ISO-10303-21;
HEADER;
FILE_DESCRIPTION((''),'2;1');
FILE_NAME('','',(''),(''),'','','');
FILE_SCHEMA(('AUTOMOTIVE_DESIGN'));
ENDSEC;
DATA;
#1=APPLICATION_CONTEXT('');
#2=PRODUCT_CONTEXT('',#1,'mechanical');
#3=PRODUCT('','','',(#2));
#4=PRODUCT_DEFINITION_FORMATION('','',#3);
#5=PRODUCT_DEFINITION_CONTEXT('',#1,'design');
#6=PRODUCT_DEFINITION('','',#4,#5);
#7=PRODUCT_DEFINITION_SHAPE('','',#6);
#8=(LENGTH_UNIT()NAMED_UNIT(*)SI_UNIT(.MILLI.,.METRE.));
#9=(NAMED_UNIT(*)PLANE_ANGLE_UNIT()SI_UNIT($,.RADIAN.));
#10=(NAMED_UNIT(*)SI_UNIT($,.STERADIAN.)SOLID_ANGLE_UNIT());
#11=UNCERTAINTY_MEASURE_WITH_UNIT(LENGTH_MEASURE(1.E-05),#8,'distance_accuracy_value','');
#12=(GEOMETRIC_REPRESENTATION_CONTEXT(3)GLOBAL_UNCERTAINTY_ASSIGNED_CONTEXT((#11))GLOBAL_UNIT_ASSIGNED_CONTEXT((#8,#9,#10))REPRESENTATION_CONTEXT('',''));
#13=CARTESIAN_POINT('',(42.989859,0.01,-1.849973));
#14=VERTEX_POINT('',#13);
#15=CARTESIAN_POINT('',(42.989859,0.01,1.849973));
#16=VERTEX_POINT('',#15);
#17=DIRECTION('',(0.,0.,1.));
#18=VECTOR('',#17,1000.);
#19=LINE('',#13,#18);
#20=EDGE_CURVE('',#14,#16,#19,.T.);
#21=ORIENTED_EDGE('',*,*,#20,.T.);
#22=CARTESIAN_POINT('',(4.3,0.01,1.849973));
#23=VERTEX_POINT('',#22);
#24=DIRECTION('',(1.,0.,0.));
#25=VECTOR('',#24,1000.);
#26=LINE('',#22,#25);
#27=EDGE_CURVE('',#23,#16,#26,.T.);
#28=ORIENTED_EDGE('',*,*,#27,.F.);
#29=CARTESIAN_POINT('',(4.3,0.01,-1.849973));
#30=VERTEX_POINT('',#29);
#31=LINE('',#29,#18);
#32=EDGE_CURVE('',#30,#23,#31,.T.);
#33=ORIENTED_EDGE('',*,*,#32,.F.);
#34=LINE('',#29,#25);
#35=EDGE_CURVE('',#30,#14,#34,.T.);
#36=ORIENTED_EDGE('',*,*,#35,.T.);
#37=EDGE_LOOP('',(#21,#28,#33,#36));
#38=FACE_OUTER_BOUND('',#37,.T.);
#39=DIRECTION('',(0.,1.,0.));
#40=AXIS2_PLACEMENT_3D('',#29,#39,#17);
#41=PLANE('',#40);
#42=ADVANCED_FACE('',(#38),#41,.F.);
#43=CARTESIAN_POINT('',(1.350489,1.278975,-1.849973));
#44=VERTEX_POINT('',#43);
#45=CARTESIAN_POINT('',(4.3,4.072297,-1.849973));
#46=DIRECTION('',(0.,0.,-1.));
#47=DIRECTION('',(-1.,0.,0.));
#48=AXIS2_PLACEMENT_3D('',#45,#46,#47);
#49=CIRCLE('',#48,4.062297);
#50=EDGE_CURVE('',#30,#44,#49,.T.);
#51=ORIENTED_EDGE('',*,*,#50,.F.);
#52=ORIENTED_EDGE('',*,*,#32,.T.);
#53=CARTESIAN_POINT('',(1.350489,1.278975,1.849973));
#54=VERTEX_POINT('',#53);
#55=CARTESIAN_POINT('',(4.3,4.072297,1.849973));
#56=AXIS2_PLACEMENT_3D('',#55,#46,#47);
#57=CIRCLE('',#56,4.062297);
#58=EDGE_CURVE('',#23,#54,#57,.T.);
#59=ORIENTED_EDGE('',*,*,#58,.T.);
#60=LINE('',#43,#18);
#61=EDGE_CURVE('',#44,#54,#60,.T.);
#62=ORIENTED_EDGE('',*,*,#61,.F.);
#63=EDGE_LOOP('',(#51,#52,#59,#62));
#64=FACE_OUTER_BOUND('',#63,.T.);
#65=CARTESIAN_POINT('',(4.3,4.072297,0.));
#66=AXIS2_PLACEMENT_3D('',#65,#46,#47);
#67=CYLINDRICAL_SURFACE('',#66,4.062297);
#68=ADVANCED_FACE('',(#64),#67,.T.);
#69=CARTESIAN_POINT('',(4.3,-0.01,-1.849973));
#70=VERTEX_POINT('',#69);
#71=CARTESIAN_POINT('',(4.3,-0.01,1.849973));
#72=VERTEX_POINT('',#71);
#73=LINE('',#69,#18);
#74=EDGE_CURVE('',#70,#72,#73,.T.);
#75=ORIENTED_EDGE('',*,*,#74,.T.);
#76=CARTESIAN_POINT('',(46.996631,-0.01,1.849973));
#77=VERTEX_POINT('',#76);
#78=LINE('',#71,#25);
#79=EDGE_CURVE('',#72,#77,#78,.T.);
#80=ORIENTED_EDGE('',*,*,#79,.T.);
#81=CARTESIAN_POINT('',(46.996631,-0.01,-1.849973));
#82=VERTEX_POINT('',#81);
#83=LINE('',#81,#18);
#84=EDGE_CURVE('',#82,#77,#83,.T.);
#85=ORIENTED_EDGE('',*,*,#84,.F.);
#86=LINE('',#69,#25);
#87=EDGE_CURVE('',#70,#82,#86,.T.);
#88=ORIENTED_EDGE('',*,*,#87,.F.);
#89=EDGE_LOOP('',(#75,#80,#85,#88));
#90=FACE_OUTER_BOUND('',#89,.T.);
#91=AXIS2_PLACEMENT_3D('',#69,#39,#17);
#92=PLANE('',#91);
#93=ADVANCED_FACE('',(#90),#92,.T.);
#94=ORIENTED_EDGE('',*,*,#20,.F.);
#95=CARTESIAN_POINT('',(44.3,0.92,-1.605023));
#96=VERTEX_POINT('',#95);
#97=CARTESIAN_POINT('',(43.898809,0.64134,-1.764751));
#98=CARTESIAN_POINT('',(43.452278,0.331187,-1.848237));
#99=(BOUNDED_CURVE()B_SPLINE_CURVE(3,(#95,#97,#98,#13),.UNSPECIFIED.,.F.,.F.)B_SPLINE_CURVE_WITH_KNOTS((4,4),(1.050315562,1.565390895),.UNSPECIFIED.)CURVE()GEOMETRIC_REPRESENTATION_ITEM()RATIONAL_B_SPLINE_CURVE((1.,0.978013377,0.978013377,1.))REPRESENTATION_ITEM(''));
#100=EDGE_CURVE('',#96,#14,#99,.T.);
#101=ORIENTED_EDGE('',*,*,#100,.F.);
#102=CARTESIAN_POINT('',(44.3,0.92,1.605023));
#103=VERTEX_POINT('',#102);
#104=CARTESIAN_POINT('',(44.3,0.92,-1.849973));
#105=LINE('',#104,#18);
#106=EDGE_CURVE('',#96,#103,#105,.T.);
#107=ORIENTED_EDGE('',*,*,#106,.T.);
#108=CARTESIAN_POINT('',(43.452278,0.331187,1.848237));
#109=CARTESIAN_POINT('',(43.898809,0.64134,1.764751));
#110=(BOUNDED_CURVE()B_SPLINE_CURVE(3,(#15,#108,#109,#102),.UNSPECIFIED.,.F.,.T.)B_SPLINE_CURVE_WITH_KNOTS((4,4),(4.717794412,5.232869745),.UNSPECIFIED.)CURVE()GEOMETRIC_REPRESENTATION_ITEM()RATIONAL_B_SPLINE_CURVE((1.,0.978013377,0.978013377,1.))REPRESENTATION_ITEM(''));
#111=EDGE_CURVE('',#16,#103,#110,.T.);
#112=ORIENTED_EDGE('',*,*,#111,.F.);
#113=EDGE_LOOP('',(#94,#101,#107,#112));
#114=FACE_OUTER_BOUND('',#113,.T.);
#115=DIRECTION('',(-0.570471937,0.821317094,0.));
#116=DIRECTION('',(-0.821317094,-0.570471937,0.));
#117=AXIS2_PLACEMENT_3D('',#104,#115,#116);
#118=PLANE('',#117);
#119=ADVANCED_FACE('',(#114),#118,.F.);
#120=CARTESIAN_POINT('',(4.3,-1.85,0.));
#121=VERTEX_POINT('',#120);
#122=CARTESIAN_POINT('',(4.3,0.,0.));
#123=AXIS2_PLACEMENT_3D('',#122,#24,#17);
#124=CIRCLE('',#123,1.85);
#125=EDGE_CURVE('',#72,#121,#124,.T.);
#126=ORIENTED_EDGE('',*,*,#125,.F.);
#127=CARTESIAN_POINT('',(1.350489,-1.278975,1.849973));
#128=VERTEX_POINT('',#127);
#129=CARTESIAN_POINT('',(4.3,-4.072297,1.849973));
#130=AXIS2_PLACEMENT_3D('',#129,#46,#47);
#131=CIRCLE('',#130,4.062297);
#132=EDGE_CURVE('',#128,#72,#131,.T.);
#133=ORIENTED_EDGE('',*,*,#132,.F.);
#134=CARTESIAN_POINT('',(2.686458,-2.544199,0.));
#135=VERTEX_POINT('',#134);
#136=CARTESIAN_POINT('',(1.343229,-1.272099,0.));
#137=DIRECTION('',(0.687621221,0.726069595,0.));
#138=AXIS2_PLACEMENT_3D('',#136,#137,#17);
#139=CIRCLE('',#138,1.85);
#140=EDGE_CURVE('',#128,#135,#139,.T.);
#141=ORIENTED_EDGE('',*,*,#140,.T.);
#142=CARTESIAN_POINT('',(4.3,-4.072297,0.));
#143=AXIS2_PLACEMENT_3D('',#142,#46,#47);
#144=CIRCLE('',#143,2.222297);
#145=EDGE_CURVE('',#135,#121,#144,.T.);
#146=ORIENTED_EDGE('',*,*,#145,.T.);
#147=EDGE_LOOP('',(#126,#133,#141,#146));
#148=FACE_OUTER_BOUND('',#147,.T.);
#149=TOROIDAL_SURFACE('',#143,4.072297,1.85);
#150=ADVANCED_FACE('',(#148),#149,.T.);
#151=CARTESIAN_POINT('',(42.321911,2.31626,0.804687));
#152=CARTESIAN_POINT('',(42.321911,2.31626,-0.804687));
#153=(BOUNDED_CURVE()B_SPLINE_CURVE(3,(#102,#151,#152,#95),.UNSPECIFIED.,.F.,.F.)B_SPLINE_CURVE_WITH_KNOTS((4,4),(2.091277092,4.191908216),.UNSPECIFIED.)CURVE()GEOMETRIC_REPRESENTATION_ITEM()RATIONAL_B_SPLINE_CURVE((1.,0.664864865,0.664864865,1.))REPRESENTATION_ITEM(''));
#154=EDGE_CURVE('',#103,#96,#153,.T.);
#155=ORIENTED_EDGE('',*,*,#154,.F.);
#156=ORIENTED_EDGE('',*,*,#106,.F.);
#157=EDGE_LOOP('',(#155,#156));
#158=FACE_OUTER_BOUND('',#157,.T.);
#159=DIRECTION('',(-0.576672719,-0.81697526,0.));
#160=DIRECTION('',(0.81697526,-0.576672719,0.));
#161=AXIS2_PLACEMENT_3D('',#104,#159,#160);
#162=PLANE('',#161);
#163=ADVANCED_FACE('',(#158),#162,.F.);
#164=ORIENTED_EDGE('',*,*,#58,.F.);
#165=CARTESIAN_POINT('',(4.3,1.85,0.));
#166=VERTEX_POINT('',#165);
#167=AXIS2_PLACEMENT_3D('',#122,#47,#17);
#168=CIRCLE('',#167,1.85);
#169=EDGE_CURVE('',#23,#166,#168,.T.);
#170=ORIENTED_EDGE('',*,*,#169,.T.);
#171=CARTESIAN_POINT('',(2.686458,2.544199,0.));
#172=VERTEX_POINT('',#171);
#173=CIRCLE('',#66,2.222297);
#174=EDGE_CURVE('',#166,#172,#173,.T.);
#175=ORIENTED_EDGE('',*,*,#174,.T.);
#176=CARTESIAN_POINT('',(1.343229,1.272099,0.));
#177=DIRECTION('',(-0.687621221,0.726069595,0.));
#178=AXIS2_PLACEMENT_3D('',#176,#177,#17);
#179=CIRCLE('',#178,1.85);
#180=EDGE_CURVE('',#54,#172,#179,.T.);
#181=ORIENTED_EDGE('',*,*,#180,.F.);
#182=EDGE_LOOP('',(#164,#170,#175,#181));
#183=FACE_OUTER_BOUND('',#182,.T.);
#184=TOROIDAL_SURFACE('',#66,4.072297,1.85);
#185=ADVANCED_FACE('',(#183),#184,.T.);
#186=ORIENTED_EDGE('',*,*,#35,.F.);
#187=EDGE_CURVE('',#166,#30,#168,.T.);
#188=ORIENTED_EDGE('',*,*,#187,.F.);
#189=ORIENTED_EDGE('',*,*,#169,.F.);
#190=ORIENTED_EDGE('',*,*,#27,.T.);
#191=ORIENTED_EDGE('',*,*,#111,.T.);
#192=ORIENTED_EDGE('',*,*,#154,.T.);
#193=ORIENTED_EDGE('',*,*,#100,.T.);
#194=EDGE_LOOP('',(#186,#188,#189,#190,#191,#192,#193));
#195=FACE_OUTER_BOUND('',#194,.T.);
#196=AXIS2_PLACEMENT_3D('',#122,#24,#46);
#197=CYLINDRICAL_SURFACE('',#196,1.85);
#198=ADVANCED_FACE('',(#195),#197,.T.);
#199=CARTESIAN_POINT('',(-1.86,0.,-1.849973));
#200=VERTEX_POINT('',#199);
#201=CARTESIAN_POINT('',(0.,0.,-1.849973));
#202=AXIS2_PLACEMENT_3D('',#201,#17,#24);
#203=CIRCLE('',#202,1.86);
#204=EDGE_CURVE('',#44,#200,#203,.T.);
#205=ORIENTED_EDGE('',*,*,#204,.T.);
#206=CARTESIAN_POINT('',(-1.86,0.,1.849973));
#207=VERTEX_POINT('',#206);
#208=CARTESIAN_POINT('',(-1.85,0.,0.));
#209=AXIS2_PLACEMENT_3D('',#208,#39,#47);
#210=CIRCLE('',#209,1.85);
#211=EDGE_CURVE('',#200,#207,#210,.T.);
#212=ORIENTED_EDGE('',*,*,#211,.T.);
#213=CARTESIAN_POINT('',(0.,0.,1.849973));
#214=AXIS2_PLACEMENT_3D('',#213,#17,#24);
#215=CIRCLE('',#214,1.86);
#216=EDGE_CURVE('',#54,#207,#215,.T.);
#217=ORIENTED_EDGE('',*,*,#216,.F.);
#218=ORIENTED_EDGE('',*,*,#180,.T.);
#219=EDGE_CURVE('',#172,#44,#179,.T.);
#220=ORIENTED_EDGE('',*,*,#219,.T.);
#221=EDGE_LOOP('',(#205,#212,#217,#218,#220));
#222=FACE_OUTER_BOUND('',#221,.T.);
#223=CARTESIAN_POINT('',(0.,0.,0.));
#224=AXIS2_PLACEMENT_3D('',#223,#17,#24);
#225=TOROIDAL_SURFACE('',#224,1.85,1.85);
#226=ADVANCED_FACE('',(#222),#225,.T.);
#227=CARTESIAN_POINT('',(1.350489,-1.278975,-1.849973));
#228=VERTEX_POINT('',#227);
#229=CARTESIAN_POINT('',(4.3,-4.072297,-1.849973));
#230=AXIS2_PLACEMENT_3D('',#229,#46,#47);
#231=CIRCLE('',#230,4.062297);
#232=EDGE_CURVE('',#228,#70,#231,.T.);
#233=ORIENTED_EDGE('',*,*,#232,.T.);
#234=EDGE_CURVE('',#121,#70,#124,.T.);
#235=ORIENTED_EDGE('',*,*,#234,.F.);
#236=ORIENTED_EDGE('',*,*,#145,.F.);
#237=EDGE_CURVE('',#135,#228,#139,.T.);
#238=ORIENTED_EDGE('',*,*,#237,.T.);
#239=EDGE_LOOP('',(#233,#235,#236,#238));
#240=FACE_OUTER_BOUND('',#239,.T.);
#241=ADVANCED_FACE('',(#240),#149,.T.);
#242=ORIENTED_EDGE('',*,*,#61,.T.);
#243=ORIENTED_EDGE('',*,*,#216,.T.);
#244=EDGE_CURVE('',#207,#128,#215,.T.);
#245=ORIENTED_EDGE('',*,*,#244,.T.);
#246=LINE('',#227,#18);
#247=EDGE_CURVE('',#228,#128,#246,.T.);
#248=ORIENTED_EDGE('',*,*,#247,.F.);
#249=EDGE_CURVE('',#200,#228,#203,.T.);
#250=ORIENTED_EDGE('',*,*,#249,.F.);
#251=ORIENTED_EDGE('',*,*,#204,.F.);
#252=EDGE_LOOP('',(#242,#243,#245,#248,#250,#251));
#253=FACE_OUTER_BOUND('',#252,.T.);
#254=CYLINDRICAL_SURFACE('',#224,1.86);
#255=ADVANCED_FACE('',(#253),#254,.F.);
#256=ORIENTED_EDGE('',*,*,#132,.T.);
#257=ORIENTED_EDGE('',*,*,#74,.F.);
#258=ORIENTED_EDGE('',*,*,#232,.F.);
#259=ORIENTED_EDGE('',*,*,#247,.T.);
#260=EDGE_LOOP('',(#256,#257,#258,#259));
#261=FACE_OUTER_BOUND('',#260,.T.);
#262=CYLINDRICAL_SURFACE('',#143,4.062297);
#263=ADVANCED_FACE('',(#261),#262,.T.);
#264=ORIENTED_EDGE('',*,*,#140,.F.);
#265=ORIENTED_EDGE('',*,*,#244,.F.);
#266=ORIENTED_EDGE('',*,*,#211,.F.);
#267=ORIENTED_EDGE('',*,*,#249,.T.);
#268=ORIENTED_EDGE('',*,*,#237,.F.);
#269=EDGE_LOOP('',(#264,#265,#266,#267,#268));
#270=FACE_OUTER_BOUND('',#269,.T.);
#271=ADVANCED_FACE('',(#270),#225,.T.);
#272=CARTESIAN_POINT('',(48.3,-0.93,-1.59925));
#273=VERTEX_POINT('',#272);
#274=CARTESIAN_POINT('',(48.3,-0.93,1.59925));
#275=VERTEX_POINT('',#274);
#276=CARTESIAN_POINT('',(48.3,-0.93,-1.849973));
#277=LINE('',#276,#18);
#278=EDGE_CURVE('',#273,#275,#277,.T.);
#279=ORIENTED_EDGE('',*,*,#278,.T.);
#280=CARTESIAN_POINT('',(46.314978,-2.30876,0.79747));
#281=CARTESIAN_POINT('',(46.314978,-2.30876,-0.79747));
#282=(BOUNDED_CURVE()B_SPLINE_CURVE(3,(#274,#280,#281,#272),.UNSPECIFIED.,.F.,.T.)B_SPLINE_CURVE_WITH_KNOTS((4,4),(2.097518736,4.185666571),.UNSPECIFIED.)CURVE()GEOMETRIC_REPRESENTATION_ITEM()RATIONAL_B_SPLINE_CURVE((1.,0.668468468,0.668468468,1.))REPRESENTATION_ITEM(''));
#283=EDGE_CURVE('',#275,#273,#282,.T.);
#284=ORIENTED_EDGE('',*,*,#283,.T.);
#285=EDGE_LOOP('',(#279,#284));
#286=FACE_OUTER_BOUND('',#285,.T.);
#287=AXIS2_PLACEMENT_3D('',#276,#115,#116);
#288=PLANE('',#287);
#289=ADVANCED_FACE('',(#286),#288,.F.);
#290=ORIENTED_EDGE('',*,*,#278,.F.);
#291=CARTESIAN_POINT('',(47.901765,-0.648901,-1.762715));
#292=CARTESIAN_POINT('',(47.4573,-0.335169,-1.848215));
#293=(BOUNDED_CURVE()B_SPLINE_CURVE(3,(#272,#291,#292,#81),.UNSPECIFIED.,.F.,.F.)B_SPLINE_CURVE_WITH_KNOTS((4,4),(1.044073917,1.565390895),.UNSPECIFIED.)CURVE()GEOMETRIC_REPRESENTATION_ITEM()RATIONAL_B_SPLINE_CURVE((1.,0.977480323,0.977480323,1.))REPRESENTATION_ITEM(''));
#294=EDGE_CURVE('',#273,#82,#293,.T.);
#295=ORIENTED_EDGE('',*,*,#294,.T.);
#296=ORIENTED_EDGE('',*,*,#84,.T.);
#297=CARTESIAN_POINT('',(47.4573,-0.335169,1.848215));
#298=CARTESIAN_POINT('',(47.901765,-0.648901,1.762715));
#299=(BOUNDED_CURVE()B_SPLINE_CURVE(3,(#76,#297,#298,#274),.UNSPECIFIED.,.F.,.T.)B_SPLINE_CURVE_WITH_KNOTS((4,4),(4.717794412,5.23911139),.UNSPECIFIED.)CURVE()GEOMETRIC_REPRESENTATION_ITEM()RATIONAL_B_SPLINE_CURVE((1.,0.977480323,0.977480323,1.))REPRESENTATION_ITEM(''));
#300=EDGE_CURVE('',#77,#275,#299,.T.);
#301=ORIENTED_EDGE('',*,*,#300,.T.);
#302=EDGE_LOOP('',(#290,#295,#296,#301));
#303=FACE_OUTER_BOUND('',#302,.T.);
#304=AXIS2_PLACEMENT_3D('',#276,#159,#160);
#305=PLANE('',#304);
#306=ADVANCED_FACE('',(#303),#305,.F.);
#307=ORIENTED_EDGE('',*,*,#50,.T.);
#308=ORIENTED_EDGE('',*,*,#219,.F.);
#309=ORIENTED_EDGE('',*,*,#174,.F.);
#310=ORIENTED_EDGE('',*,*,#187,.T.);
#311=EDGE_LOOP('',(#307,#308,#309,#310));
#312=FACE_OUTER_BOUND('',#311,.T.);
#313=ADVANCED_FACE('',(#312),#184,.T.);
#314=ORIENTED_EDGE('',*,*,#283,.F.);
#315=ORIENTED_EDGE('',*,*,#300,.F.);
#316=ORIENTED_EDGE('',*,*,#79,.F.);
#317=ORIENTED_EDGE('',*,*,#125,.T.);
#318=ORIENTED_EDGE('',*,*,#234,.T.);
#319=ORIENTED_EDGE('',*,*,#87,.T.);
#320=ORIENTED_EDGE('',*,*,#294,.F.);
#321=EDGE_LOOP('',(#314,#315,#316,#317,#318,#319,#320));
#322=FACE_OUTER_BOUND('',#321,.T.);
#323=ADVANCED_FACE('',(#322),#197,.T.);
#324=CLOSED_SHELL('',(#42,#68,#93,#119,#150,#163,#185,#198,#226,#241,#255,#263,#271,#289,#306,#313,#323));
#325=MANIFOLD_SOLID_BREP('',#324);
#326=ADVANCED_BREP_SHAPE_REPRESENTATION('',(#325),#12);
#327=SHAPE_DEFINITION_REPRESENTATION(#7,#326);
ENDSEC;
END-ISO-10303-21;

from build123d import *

# Parameters (mm, degrees)
CUT_EXTRUDE_1_DEPTH      = 49.47682334
CUT_EXTRUDE_1_DEPTH_BACK = 49.47682334


with BuildPart() as part:
    # 扫描2: sweep along a path in Sketch 203
    with BuildLine(Plane.XY) as sweep_2_path:
        Line((44.3, 1.85), (4.3, 1.85))
        ThreePointArc((4.3, 1.85), (3.421730256, 2.030913567), (2.686457501, 2.544198517))
        ThreePointArc((2.686457501, 2.544198517), (-3.7, 0), (2.686457501, -2.544198517))
        ThreePointArc((2.686457501, -2.544198517), (3.421730256, -2.030913567), (4.3, -1.85))
        Line((4.3, -1.85), (48.3, -1.85))
    # 草图2 → 扫描2 (sweep)
    with BuildSketch(Plane(origin=(44.3, 1.85, 0), x_dir=(0, 0, 1), z_dir=(-1, 0, 0))):
        with BuildLine():
            Line((-1.849972973, -1.84), (1.849972973, -1.84))
            ThreePointArc((1.849972973, -1.84), (0, 0), (-1.849972973, -1.84))
        make_face()
    sweep(path=sweep_2_path.line)

    # 草图3 → 切除-拉伸1 (cut, two sides: drawn at the far end of the back side and taken through both)
    with BuildSketch(Plane.XY.offset(-CUT_EXTRUDE_1_DEPTH_BACK)):
        Polygon((44.3, 0.92), (42.982464131, 1.85), (48.31, 1.85), (48.31, -1.85), (46.975462056, -1.85), (48.3, -0.93), (46.982464131, 0), (42.975462056, 0), align=None)
    extrude(amount=CUT_EXTRUDE_1_DEPTH + CUT_EXTRUDE_1_DEPTH_BACK, mode=Mode.SUBTRACT)


solid = part.part
